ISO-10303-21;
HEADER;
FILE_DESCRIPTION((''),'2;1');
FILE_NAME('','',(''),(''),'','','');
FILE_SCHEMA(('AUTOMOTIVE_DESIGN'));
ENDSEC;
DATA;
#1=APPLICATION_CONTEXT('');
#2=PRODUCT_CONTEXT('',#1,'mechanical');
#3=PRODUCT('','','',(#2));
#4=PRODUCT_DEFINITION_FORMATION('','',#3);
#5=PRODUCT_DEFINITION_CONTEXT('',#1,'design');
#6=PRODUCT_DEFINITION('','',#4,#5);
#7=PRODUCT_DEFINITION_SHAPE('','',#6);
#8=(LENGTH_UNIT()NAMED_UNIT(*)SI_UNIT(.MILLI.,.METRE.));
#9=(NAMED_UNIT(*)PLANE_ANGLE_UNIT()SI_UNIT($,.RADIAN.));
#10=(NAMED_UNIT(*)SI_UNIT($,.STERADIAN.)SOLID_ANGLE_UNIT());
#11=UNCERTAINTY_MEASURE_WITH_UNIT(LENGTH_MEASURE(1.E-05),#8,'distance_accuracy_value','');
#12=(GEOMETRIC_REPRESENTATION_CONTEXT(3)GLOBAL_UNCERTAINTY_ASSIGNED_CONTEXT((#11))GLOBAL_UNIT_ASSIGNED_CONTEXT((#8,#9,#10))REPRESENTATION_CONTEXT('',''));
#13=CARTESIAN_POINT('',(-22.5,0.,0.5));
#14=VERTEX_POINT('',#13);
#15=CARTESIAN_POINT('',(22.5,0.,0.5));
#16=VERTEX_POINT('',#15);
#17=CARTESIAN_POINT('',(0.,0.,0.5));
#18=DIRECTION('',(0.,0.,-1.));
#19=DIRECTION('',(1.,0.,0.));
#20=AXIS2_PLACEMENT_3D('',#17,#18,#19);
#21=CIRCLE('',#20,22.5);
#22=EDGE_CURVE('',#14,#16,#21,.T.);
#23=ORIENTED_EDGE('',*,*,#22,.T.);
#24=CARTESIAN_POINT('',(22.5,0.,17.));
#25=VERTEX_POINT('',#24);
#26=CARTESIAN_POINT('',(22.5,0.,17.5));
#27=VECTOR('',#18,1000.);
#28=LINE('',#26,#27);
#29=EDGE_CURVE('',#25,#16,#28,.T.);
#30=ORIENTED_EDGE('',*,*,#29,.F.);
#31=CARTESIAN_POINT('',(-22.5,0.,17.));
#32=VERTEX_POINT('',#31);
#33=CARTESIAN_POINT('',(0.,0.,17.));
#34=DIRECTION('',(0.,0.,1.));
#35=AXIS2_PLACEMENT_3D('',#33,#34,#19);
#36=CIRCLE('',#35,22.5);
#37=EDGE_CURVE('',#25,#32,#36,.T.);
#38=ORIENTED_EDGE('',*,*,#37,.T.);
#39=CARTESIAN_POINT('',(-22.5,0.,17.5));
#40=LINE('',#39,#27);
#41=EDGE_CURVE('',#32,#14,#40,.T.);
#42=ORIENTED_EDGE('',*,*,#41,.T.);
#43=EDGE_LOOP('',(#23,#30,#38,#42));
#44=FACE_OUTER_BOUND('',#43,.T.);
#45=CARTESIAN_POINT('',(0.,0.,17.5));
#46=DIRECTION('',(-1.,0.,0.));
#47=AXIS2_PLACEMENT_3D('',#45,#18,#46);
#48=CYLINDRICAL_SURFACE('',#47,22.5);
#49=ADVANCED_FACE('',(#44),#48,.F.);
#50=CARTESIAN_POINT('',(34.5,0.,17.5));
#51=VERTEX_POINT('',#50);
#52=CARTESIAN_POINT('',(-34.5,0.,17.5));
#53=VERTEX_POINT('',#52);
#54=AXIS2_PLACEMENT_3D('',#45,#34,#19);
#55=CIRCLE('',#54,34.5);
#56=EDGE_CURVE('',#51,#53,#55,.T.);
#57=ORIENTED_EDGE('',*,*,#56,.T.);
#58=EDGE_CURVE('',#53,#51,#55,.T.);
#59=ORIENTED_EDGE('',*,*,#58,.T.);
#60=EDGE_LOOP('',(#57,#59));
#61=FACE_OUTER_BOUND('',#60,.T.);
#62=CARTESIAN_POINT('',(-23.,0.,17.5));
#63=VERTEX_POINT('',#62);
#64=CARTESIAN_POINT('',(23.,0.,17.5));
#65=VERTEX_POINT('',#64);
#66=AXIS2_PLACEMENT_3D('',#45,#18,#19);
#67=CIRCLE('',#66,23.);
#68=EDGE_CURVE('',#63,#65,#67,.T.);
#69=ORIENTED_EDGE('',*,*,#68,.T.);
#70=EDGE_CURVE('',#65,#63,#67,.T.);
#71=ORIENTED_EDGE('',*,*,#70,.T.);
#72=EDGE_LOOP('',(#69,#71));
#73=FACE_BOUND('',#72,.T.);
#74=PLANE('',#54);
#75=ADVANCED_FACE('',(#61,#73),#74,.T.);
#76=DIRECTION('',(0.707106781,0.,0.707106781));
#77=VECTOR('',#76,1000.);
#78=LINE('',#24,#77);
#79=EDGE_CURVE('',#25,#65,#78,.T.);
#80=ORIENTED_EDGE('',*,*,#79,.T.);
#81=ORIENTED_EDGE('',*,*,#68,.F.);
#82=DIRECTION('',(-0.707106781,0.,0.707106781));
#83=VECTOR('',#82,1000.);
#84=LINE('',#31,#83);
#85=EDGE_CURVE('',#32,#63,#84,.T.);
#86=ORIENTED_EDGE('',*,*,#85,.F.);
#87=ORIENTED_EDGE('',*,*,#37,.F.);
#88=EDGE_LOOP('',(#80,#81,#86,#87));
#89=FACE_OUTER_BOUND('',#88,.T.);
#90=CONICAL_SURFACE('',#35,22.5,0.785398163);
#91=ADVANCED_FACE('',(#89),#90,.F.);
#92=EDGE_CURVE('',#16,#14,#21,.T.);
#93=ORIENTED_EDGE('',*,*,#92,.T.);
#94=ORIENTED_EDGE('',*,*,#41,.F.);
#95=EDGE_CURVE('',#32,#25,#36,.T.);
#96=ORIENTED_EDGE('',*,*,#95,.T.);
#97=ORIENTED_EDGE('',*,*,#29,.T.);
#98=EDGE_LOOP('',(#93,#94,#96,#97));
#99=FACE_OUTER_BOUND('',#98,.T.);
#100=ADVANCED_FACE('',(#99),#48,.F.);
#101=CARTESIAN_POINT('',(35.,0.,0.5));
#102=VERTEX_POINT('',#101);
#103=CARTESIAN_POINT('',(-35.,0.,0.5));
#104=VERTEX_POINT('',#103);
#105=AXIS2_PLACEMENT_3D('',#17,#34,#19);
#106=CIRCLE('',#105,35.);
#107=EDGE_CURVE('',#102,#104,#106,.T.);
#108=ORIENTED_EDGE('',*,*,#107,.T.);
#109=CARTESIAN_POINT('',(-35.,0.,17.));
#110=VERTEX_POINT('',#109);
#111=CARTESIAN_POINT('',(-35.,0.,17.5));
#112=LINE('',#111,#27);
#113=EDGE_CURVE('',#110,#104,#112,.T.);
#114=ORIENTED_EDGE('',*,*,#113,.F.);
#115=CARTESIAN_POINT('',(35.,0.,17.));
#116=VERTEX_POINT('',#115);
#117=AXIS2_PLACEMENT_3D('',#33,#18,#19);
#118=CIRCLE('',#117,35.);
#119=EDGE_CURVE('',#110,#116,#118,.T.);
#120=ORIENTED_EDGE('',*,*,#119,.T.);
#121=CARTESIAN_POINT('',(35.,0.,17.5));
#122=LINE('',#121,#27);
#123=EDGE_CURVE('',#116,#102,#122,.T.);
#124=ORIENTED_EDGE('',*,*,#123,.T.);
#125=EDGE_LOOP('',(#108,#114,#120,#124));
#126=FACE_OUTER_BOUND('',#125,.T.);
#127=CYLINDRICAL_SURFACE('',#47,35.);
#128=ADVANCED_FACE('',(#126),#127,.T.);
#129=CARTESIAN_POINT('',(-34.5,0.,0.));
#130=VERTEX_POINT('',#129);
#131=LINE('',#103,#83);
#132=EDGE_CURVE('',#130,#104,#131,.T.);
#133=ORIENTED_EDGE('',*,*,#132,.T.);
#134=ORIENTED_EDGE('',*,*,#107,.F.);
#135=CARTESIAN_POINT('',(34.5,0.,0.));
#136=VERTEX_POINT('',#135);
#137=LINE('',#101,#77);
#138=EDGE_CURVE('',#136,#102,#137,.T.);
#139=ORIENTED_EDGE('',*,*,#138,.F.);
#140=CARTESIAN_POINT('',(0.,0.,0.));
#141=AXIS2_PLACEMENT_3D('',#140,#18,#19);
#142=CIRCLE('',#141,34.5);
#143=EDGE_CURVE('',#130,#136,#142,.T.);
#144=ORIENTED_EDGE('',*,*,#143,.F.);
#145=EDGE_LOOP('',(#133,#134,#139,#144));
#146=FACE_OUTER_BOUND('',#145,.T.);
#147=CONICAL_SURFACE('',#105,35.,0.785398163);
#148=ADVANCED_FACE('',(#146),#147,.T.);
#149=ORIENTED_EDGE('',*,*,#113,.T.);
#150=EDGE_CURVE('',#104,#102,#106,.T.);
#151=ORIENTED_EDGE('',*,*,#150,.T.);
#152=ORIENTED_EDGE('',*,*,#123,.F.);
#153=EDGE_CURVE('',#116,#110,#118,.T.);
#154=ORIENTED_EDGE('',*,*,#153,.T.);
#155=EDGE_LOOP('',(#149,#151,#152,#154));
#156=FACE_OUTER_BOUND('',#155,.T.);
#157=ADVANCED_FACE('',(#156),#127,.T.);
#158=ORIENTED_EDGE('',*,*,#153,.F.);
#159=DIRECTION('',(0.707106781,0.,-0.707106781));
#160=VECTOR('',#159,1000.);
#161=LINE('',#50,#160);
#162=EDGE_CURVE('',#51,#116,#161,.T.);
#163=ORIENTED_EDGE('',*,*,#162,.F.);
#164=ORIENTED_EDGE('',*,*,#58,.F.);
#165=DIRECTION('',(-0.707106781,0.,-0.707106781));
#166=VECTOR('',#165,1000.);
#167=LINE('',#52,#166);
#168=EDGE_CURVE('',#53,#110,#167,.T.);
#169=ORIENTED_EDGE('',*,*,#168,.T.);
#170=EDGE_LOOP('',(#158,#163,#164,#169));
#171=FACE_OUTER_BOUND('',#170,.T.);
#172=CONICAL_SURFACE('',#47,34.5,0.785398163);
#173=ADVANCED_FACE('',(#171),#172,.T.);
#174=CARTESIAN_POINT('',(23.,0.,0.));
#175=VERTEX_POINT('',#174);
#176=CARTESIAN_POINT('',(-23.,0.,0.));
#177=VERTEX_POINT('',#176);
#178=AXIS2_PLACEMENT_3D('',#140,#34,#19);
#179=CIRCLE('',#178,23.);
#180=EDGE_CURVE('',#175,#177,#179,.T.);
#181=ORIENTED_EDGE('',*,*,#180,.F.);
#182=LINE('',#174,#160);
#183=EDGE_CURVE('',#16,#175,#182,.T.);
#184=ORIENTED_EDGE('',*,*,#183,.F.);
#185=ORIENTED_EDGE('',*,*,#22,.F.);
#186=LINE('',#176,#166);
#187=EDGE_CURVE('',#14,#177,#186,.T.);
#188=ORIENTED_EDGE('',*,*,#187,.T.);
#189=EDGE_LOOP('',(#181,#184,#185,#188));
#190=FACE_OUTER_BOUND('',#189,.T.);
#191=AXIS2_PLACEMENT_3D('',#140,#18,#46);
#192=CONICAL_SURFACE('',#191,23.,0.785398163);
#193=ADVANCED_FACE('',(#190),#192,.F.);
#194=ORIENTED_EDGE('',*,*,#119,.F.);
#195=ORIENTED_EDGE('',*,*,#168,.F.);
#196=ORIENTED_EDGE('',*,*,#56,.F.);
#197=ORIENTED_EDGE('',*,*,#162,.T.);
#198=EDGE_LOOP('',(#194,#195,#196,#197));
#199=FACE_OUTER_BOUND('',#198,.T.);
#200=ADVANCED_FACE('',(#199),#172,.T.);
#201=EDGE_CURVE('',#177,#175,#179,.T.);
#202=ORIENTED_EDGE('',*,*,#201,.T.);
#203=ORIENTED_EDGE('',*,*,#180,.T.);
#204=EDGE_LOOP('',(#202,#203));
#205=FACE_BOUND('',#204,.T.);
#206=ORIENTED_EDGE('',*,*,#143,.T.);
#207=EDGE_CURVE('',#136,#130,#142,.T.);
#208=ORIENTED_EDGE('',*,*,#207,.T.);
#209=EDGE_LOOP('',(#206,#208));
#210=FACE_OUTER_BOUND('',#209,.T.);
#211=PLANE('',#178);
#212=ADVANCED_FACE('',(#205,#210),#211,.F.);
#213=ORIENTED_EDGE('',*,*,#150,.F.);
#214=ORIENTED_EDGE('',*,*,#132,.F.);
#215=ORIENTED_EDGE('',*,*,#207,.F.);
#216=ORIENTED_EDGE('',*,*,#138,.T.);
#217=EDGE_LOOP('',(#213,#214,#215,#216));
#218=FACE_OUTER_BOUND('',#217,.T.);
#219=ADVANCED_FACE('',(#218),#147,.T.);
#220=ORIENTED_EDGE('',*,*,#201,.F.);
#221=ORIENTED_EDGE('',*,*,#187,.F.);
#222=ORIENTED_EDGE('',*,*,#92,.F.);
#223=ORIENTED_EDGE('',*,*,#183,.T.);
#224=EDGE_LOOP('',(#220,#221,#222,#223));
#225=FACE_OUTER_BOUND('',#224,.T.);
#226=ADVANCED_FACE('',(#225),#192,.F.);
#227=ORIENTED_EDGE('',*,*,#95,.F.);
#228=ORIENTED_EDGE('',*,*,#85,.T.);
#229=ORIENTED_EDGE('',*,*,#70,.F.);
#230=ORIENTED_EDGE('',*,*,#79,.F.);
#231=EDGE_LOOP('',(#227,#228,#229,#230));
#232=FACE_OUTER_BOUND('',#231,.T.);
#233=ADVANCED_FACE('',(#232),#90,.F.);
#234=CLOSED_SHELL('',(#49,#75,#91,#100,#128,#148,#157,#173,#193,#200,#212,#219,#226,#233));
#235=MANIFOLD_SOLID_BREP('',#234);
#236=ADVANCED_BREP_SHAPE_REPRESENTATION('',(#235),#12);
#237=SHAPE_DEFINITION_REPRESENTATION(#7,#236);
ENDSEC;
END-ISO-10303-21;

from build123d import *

# Parameters (mm, degrees)
SKETCH_1_R      = 35
SKETCH_1_R_2    = 22.5
EXTRUDE_1_DEPTH = 17.5
CHAMFER_1_SIZE  = 0.5


with BuildPart() as part:
    # 草图1 → 凸台-拉伸1 (new body)
    with BuildSketch(Plane.XY):
        Circle(SKETCH_1_R)
        Circle(SKETCH_1_R_2, mode=Mode.SUBTRACT)
    extrude(amount=EXTRUDE_1_DEPTH)

    # 倒角1
    chamfer_1_edges = [part.edges().sort_by_distance(p)[0] for p in [
        (-35, 0, 0),
        (-35, 0, 17.5),
        (-22.5, 0, 0),
        (-22.5, 0, 17.5),
    ]]
    chamfer(chamfer_1_edges, length=CHAMFER_1_SIZE)


solid = part.part
